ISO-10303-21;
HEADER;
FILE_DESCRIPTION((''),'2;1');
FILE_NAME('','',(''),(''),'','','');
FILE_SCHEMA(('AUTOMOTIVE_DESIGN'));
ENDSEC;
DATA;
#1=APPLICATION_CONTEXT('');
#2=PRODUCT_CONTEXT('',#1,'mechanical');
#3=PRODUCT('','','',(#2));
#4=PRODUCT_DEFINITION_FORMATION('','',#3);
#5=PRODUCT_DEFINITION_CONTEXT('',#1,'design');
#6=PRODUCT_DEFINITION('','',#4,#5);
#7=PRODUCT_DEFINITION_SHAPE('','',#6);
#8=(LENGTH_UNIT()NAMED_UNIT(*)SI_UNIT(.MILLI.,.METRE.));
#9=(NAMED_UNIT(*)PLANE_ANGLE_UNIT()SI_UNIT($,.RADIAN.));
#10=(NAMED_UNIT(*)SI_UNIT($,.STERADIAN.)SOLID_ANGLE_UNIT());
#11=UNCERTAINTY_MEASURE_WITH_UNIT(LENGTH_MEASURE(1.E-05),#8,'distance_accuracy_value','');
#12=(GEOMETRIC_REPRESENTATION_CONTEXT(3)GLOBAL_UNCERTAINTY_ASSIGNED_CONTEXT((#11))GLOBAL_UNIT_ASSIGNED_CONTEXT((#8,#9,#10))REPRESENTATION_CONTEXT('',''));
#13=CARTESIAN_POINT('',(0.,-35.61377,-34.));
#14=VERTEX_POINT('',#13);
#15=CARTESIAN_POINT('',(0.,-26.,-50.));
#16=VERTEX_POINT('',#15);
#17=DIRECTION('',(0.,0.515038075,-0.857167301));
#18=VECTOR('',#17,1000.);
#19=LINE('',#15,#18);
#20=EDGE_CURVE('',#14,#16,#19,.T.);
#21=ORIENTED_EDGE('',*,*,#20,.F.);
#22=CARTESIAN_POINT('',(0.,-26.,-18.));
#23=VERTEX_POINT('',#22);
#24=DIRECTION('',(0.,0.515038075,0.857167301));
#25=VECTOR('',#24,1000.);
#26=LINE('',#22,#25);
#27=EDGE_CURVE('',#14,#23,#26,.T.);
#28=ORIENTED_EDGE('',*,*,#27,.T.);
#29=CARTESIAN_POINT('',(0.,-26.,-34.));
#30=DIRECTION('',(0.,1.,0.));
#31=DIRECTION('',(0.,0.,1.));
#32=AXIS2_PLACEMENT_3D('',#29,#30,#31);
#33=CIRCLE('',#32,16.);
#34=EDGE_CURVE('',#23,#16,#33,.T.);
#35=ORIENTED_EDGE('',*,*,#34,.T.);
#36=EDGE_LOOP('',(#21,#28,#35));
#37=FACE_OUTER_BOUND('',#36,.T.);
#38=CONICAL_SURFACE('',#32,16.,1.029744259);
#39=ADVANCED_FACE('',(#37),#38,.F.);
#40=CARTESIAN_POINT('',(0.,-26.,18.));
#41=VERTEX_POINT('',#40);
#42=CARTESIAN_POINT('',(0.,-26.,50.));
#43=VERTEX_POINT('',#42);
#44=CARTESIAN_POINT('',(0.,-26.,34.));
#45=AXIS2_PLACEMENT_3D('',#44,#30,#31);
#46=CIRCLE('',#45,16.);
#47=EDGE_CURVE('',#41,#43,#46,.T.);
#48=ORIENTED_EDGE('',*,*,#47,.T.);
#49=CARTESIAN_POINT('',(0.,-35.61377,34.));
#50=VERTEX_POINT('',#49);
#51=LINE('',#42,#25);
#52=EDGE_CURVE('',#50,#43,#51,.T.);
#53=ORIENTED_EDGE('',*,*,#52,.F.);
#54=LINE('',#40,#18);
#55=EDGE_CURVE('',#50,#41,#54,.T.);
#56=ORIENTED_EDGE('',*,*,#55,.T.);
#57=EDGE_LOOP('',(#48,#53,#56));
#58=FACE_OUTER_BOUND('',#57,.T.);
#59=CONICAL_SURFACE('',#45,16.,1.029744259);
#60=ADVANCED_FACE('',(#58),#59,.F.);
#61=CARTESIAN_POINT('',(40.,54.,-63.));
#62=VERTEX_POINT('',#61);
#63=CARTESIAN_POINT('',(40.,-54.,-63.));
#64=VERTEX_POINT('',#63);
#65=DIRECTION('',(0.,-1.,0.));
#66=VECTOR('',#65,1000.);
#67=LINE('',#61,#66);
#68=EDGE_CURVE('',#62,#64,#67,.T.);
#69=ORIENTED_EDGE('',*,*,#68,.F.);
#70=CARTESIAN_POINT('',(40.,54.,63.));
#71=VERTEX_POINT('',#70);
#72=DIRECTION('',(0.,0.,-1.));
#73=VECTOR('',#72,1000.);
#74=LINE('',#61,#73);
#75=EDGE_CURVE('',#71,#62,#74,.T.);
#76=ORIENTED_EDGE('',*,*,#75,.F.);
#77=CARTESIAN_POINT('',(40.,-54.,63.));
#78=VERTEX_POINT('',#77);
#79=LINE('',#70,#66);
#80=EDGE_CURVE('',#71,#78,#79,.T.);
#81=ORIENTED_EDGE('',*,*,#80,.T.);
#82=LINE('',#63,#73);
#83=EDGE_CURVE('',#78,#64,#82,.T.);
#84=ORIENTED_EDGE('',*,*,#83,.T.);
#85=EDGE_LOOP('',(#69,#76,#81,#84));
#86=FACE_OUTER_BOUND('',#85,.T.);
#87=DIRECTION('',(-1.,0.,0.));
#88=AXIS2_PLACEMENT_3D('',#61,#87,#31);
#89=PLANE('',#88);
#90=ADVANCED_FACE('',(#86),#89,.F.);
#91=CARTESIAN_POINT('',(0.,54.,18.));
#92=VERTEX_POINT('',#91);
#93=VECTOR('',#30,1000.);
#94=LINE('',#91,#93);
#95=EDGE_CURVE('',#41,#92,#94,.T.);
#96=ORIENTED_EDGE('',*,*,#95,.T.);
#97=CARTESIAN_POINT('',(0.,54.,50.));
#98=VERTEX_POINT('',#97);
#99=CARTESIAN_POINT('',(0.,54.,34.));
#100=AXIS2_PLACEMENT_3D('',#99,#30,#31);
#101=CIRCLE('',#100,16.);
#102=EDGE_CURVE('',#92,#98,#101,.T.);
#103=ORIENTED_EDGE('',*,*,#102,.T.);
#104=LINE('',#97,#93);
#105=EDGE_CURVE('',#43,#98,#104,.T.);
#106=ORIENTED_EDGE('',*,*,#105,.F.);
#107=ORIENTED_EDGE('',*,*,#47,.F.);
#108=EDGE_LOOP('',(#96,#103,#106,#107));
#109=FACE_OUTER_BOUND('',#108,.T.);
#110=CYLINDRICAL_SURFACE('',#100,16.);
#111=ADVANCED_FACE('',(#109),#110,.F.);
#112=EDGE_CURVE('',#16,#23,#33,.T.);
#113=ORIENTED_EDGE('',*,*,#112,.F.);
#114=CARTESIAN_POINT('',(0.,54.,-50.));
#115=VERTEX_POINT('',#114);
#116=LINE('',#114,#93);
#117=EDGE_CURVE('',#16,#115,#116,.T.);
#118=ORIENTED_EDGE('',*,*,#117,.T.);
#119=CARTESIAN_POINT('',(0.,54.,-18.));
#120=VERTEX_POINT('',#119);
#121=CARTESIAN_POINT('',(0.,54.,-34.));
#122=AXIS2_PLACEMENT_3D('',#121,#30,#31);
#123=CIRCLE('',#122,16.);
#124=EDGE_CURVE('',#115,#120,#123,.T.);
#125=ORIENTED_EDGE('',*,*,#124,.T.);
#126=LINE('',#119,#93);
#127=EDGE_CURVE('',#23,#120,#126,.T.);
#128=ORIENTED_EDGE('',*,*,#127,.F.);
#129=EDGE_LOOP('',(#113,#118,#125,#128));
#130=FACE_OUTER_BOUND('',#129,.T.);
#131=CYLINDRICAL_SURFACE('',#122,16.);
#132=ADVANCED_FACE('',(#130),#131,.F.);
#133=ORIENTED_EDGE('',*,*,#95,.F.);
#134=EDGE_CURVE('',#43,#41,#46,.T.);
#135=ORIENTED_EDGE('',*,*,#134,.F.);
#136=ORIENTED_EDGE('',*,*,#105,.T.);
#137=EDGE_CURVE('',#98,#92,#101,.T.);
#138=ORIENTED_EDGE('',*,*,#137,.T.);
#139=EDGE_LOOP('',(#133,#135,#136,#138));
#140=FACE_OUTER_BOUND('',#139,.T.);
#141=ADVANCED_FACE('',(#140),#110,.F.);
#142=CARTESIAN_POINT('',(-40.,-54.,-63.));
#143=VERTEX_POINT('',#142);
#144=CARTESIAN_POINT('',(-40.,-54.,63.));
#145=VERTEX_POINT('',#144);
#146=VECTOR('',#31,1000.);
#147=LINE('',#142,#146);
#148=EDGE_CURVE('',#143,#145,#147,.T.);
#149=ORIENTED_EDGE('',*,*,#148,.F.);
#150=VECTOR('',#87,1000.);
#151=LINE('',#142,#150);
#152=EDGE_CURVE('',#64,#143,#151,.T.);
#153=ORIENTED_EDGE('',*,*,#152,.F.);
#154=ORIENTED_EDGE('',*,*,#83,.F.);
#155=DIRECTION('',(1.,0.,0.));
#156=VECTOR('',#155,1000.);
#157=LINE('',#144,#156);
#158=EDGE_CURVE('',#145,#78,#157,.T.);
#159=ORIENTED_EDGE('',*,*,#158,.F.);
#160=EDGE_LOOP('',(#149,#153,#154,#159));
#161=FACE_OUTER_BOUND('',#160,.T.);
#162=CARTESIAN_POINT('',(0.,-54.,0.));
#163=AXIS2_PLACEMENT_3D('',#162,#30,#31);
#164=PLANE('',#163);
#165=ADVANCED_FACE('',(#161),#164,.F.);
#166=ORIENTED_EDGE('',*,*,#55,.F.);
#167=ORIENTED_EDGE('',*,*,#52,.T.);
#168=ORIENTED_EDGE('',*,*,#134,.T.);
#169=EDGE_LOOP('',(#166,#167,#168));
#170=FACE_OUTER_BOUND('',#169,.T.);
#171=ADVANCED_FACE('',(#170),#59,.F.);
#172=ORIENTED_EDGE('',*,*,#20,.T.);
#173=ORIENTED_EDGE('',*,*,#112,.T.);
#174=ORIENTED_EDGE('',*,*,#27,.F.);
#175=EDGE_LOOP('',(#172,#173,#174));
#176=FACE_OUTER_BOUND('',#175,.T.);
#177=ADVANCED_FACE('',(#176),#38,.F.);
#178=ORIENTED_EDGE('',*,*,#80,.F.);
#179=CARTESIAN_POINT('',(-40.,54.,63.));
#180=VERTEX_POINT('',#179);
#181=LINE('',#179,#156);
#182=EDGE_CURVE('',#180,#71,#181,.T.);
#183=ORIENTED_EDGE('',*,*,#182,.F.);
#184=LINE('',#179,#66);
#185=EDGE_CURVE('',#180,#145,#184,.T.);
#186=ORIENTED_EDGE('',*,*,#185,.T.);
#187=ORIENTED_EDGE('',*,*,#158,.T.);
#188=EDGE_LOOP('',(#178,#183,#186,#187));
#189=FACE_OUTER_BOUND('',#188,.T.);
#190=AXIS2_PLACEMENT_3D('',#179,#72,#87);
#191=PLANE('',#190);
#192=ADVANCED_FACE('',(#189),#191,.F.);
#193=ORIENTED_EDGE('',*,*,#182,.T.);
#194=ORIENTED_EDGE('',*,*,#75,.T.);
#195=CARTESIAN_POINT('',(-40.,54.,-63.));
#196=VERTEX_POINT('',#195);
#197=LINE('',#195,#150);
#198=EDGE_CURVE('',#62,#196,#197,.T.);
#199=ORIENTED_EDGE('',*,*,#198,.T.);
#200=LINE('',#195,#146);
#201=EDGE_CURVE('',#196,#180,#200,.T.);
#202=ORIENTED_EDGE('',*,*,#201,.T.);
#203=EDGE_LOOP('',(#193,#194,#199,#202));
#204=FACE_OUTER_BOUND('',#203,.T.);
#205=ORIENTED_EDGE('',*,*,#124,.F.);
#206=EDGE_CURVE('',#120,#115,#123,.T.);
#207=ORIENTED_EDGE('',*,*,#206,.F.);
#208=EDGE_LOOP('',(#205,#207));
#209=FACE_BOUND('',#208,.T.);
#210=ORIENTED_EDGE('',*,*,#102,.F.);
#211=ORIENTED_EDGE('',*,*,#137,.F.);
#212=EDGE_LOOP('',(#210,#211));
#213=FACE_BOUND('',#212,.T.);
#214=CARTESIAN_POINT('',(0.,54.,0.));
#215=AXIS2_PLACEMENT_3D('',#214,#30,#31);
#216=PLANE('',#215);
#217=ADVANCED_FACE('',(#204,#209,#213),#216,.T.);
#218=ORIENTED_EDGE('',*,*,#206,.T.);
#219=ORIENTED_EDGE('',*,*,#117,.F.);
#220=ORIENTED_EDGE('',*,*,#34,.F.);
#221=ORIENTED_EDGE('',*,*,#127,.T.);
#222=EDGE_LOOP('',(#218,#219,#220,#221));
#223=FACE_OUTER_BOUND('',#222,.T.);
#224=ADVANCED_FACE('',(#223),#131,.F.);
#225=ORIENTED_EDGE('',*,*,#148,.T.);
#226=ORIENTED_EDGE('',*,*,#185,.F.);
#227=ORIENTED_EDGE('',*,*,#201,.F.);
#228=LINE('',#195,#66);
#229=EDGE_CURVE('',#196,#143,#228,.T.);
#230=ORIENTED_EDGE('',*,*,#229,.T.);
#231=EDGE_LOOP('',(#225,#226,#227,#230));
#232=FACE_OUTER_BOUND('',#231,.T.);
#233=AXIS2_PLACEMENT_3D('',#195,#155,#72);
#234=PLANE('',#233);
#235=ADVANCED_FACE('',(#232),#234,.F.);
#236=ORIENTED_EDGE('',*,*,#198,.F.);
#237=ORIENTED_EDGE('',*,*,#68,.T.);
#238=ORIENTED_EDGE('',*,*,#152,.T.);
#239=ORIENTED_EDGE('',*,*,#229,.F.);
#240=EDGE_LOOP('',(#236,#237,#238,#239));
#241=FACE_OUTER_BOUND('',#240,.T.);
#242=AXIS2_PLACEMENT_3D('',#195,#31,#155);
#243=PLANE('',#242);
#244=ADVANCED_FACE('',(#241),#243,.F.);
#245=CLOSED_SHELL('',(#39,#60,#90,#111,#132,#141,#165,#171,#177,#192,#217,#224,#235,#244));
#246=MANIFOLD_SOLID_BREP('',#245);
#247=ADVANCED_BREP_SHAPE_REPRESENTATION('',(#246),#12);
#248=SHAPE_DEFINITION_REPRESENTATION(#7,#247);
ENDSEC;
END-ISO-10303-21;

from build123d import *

# Parameters (mm, degrees)
SKETCH2_W              = 80
SKETCH2_H              = 126
BOSS_EXTRUDE1_DEPTH    = 54
M36_TAPPED_HOLE1_D     = 32
M36_TAPPED_HOLE1_DEPTH = 80
M36_TAPPED_HOLE1_TIP   = 9.613769904


with BuildPart() as part:
    # Sketch2 → Boss-Extrude1 (new, symmetric)
    with BuildSketch(Plane(origin=(0, 0, 0), x_dir=(1, 0, 0), z_dir=(0, 1, 0))):
        Rectangle(SKETCH2_W, SKETCH2_H)
    extrude(amount=BOSS_EXTRUDE1_DEPTH, both=True)

    # M36 Tapped Hole1
    with Locations(Plane(origin=(0, 54, 0), x_dir=(1, 0, 0), z_dir=(0, 1, 0))):
        with Locations((0, 34), (0, -34)):
            Hole(M36_TAPPED_HOLE1_D / 2, depth=M36_TAPPED_HOLE1_DEPTH)
            with Locations((0, 0, -(M36_TAPPED_HOLE1_DEPTH + M36_TAPPED_HOLE1_TIP / 2))):  # 118° drill point
                Cone(0, M36_TAPPED_HOLE1_D / 2, M36_TAPPED_HOLE1_TIP, mode=Mode.SUBTRACT)


solid = part.part
